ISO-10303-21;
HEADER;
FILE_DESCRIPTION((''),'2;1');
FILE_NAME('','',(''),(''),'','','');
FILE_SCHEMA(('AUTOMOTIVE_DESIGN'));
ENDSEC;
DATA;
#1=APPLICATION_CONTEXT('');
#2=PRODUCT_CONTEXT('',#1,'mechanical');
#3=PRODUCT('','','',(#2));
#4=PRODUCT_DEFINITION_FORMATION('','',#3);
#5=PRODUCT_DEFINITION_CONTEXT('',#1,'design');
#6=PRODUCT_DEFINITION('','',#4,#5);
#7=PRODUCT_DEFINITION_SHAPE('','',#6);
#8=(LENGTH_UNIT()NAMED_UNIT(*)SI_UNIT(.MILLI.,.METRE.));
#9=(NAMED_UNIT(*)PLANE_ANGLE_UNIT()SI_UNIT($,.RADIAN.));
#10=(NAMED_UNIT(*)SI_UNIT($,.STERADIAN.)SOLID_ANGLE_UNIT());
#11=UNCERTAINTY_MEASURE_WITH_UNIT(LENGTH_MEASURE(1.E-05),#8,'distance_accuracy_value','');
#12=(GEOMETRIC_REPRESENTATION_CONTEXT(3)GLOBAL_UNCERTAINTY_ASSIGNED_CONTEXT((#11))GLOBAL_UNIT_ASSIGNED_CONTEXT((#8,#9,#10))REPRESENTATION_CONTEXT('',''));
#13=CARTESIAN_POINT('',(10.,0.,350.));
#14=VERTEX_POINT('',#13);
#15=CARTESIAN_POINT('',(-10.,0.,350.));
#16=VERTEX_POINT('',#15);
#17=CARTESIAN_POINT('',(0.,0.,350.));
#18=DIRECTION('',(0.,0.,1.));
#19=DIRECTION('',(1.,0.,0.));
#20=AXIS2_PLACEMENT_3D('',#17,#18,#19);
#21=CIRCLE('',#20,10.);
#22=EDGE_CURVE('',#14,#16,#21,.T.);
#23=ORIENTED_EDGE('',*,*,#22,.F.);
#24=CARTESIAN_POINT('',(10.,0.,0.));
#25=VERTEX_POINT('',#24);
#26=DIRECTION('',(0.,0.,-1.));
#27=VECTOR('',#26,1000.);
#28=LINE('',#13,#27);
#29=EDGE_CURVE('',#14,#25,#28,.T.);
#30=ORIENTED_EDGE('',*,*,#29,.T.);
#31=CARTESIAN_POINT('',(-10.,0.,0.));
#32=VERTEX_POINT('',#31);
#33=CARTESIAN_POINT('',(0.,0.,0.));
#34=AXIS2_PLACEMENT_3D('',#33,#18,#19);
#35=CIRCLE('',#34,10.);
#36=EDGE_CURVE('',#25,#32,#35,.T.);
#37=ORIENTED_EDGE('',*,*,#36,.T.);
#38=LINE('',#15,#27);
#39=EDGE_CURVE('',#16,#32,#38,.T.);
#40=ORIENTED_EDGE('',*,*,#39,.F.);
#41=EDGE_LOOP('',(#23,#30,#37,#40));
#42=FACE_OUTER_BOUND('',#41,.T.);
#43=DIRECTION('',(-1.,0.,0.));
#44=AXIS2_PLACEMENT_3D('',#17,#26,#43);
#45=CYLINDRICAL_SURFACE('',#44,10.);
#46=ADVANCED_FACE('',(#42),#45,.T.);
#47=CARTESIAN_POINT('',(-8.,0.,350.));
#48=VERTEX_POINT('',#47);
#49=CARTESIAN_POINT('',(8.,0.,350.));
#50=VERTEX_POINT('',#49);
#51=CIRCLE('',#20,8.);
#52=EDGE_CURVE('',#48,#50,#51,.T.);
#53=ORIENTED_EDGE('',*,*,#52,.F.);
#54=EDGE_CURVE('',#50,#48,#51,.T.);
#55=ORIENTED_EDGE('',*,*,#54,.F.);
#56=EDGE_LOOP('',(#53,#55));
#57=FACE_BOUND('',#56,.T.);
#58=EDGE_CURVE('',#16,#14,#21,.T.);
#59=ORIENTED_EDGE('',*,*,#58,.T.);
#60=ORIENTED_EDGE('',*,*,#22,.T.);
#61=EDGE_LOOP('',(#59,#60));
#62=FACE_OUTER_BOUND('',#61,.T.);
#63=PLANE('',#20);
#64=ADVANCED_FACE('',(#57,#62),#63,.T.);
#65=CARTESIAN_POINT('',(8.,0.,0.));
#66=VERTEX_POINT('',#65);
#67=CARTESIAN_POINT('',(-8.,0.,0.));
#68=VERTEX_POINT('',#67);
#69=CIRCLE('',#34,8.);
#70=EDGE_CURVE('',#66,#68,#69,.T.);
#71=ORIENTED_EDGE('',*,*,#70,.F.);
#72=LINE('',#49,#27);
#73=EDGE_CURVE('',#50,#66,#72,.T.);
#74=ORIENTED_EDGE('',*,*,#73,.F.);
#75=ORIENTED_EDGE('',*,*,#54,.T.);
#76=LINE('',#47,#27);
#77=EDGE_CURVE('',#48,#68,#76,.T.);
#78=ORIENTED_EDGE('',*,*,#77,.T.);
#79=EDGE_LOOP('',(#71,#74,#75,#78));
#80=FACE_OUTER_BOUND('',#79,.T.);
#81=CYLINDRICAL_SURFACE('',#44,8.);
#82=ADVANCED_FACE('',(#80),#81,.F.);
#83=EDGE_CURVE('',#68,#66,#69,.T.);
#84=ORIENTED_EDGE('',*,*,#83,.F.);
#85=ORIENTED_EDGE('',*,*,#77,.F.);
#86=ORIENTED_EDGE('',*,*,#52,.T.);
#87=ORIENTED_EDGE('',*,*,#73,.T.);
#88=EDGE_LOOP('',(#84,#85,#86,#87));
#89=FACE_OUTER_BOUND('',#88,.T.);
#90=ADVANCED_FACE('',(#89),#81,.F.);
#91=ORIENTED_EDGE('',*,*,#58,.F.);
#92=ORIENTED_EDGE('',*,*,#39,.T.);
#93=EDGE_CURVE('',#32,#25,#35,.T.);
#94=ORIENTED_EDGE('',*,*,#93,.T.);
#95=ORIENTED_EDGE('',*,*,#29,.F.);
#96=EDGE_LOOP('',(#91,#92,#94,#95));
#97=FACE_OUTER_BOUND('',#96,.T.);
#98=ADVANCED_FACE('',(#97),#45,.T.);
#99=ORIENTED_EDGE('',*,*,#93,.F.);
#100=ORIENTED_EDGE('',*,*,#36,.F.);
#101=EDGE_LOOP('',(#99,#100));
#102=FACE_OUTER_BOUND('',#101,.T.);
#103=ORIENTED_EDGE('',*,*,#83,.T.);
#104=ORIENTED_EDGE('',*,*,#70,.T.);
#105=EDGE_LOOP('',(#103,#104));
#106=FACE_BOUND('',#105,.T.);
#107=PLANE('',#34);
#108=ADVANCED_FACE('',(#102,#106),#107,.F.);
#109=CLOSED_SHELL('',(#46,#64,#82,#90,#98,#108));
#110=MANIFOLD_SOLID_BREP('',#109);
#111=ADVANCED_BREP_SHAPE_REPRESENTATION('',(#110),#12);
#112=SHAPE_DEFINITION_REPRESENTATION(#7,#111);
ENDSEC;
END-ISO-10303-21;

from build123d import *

# Parameters (mm, degrees)
SKETCH_1_R      = 10
SKETCH_1_R_2    = 8
EXTRUDE_1_DEPTH = 350


with BuildPart() as part:
    # 草图1 → 拉伸-薄壁1 (new body)
    with BuildSketch(Plane.XY):
        Circle(SKETCH_1_R)
        Circle(SKETCH_1_R_2, mode=Mode.SUBTRACT)
    extrude(amount=EXTRUDE_1_DEPTH)


solid = part.part
